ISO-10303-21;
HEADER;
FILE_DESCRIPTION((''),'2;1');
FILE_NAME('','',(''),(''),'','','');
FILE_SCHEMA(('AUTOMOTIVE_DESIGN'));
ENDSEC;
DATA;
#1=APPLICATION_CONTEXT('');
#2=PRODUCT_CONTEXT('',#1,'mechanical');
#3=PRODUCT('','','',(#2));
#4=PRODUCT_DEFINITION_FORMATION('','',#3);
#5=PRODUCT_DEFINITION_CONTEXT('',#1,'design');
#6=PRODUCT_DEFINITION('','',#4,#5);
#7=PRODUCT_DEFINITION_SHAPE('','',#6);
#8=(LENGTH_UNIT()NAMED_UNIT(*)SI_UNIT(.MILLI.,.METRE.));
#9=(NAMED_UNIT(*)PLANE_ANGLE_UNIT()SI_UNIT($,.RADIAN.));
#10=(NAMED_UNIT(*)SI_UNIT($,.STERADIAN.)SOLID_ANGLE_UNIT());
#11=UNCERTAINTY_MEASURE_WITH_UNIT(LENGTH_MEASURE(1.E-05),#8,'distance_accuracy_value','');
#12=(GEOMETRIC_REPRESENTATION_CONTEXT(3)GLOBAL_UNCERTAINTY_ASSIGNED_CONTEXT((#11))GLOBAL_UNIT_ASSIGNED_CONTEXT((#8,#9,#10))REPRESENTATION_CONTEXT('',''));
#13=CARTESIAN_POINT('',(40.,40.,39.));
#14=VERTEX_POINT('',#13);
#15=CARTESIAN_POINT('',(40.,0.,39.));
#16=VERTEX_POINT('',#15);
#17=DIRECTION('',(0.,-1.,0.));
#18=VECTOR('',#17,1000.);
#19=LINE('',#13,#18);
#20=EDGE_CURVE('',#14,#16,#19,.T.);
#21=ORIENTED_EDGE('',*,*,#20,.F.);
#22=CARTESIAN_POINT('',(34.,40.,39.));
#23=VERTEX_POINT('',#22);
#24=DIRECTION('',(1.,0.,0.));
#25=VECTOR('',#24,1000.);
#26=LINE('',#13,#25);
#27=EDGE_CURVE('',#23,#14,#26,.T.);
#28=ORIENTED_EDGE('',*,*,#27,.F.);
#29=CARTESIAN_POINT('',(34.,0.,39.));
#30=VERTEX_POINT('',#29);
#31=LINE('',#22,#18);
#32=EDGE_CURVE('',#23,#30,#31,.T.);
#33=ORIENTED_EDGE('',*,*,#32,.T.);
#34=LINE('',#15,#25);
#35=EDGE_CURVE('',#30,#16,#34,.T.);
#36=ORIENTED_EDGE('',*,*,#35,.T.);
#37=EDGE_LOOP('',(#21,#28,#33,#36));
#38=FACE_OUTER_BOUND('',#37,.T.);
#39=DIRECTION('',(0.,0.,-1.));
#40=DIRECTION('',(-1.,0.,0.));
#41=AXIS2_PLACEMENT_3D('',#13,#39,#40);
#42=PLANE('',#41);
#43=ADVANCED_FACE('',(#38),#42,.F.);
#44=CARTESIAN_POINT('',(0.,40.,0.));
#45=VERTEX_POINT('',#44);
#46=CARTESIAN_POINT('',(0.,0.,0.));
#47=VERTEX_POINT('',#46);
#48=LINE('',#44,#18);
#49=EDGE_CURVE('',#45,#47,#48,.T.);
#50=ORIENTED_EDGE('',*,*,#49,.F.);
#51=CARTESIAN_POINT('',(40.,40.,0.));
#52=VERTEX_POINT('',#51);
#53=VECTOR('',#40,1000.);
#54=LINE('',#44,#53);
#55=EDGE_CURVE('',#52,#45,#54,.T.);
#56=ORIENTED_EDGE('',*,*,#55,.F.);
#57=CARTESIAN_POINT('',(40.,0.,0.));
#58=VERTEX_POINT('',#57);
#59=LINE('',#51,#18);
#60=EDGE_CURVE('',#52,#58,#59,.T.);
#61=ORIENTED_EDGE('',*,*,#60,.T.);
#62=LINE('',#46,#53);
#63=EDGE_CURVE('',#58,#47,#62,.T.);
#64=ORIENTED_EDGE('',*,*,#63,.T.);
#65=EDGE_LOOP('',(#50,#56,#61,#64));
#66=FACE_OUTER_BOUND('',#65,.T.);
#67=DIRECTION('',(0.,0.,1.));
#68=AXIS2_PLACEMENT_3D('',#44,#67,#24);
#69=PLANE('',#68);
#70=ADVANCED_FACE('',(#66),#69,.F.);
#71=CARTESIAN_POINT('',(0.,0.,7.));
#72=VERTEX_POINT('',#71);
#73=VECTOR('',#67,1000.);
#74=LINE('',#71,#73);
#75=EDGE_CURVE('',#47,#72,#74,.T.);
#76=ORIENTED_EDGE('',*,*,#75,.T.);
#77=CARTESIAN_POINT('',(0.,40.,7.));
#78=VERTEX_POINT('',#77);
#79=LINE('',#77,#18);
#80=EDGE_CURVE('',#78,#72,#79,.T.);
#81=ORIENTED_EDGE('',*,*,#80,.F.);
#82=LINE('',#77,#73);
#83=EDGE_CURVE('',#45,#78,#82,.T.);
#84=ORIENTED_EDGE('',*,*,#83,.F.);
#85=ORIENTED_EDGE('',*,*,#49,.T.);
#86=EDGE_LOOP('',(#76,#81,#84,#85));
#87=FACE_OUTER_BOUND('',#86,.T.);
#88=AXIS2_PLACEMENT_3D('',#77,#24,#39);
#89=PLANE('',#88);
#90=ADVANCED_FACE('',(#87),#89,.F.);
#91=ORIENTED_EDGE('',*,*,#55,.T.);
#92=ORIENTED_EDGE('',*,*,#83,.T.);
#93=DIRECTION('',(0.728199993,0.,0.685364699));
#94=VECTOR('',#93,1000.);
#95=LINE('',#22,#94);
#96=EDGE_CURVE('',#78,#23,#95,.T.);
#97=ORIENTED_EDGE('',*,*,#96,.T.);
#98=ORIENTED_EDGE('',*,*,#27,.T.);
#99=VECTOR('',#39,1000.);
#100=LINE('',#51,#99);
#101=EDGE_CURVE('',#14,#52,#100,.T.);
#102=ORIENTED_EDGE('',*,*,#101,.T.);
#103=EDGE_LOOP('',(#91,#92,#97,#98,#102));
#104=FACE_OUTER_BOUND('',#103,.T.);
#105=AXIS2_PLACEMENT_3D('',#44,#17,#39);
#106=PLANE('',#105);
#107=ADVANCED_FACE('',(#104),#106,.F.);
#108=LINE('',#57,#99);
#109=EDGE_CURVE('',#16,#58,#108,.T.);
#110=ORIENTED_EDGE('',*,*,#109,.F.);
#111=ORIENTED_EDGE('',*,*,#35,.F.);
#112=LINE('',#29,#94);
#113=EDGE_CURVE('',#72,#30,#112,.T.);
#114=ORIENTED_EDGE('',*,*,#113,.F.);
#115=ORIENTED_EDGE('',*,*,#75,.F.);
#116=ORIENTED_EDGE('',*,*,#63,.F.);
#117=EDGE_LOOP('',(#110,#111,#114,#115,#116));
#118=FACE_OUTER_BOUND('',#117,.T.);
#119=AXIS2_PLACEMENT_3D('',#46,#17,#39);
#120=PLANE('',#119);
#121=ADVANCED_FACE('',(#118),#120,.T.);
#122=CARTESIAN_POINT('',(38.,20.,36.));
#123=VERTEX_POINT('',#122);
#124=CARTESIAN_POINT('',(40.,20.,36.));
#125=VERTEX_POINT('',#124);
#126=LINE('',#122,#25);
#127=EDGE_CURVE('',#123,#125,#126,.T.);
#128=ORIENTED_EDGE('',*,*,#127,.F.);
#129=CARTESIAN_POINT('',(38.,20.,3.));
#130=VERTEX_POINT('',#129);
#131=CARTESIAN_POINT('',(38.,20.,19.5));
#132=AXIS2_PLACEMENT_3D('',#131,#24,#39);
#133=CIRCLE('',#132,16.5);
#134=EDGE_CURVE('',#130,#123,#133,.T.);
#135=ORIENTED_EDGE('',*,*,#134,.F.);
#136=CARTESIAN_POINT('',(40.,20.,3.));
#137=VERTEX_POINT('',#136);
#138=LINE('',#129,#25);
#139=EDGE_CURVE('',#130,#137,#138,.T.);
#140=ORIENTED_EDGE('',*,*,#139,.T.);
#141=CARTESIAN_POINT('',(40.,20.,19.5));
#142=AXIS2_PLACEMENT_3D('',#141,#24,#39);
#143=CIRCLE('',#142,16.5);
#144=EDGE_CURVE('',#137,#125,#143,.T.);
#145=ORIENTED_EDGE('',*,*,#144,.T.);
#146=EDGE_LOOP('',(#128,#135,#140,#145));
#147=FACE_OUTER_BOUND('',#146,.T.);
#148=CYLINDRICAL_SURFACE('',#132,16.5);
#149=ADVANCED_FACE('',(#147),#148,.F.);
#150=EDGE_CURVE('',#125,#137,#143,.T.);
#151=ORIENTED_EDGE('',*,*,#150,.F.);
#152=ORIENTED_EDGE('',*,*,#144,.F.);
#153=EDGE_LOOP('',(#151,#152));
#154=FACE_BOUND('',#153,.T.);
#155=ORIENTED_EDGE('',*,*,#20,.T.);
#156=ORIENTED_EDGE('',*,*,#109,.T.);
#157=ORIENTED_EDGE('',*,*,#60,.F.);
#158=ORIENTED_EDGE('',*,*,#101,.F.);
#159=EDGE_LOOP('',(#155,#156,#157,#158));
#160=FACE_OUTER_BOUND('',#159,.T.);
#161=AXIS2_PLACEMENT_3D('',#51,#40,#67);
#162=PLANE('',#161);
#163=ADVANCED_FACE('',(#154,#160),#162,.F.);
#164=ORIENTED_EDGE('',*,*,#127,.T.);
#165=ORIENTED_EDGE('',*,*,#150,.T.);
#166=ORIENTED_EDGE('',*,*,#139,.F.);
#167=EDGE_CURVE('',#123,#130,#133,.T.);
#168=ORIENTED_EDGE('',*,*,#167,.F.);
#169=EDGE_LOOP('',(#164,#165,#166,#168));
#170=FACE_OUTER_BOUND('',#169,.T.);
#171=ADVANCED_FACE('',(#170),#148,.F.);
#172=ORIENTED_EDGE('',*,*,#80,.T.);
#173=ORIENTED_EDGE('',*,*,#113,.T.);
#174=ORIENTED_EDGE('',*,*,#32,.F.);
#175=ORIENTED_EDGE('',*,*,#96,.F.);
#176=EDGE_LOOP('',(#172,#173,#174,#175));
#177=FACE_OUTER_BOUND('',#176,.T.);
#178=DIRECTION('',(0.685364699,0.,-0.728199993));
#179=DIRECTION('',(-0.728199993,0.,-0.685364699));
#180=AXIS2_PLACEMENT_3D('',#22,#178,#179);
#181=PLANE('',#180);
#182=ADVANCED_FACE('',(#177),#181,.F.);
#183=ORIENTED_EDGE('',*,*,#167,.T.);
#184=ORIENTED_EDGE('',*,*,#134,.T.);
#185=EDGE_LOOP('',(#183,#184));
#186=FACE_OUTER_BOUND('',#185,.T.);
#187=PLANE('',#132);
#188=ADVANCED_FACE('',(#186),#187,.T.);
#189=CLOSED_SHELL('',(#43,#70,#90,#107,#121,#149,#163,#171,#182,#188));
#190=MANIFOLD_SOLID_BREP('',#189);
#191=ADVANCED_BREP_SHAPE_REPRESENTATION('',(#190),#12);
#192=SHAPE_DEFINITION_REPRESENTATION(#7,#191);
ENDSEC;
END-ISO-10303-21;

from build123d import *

# Parameters (mm, degrees)
EXTRUDE_1_DEPTH     = 40
SKETCH_2_R          = 16.5
CUT_EXTRUDE_1_DEPTH = 2


with BuildPart() as part:
    # 草图1 → 凸台-拉伸1 (new body)
    with BuildSketch(Plane(origin=(0, 0, 0), x_dir=(1, 0, 0), z_dir=(0, 1, 0))):
        Polygon((0, 0), (40, 0), (40, -39), (34, -39), (0, -7), align=None)
    extrude(amount=EXTRUDE_1_DEPTH)

    # 草图2 → 切除-拉伸1 (cut)
    with BuildSketch(Plane(origin=(40, 0, 0), x_dir=(0, 0, -1), z_dir=(1, 0, 0))):
        with Locations((-19.5, 20)):
            Circle(SKETCH_2_R)
    extrude(amount=-CUT_EXTRUDE_1_DEPTH, mode=Mode.SUBTRACT)


solid = part.part
